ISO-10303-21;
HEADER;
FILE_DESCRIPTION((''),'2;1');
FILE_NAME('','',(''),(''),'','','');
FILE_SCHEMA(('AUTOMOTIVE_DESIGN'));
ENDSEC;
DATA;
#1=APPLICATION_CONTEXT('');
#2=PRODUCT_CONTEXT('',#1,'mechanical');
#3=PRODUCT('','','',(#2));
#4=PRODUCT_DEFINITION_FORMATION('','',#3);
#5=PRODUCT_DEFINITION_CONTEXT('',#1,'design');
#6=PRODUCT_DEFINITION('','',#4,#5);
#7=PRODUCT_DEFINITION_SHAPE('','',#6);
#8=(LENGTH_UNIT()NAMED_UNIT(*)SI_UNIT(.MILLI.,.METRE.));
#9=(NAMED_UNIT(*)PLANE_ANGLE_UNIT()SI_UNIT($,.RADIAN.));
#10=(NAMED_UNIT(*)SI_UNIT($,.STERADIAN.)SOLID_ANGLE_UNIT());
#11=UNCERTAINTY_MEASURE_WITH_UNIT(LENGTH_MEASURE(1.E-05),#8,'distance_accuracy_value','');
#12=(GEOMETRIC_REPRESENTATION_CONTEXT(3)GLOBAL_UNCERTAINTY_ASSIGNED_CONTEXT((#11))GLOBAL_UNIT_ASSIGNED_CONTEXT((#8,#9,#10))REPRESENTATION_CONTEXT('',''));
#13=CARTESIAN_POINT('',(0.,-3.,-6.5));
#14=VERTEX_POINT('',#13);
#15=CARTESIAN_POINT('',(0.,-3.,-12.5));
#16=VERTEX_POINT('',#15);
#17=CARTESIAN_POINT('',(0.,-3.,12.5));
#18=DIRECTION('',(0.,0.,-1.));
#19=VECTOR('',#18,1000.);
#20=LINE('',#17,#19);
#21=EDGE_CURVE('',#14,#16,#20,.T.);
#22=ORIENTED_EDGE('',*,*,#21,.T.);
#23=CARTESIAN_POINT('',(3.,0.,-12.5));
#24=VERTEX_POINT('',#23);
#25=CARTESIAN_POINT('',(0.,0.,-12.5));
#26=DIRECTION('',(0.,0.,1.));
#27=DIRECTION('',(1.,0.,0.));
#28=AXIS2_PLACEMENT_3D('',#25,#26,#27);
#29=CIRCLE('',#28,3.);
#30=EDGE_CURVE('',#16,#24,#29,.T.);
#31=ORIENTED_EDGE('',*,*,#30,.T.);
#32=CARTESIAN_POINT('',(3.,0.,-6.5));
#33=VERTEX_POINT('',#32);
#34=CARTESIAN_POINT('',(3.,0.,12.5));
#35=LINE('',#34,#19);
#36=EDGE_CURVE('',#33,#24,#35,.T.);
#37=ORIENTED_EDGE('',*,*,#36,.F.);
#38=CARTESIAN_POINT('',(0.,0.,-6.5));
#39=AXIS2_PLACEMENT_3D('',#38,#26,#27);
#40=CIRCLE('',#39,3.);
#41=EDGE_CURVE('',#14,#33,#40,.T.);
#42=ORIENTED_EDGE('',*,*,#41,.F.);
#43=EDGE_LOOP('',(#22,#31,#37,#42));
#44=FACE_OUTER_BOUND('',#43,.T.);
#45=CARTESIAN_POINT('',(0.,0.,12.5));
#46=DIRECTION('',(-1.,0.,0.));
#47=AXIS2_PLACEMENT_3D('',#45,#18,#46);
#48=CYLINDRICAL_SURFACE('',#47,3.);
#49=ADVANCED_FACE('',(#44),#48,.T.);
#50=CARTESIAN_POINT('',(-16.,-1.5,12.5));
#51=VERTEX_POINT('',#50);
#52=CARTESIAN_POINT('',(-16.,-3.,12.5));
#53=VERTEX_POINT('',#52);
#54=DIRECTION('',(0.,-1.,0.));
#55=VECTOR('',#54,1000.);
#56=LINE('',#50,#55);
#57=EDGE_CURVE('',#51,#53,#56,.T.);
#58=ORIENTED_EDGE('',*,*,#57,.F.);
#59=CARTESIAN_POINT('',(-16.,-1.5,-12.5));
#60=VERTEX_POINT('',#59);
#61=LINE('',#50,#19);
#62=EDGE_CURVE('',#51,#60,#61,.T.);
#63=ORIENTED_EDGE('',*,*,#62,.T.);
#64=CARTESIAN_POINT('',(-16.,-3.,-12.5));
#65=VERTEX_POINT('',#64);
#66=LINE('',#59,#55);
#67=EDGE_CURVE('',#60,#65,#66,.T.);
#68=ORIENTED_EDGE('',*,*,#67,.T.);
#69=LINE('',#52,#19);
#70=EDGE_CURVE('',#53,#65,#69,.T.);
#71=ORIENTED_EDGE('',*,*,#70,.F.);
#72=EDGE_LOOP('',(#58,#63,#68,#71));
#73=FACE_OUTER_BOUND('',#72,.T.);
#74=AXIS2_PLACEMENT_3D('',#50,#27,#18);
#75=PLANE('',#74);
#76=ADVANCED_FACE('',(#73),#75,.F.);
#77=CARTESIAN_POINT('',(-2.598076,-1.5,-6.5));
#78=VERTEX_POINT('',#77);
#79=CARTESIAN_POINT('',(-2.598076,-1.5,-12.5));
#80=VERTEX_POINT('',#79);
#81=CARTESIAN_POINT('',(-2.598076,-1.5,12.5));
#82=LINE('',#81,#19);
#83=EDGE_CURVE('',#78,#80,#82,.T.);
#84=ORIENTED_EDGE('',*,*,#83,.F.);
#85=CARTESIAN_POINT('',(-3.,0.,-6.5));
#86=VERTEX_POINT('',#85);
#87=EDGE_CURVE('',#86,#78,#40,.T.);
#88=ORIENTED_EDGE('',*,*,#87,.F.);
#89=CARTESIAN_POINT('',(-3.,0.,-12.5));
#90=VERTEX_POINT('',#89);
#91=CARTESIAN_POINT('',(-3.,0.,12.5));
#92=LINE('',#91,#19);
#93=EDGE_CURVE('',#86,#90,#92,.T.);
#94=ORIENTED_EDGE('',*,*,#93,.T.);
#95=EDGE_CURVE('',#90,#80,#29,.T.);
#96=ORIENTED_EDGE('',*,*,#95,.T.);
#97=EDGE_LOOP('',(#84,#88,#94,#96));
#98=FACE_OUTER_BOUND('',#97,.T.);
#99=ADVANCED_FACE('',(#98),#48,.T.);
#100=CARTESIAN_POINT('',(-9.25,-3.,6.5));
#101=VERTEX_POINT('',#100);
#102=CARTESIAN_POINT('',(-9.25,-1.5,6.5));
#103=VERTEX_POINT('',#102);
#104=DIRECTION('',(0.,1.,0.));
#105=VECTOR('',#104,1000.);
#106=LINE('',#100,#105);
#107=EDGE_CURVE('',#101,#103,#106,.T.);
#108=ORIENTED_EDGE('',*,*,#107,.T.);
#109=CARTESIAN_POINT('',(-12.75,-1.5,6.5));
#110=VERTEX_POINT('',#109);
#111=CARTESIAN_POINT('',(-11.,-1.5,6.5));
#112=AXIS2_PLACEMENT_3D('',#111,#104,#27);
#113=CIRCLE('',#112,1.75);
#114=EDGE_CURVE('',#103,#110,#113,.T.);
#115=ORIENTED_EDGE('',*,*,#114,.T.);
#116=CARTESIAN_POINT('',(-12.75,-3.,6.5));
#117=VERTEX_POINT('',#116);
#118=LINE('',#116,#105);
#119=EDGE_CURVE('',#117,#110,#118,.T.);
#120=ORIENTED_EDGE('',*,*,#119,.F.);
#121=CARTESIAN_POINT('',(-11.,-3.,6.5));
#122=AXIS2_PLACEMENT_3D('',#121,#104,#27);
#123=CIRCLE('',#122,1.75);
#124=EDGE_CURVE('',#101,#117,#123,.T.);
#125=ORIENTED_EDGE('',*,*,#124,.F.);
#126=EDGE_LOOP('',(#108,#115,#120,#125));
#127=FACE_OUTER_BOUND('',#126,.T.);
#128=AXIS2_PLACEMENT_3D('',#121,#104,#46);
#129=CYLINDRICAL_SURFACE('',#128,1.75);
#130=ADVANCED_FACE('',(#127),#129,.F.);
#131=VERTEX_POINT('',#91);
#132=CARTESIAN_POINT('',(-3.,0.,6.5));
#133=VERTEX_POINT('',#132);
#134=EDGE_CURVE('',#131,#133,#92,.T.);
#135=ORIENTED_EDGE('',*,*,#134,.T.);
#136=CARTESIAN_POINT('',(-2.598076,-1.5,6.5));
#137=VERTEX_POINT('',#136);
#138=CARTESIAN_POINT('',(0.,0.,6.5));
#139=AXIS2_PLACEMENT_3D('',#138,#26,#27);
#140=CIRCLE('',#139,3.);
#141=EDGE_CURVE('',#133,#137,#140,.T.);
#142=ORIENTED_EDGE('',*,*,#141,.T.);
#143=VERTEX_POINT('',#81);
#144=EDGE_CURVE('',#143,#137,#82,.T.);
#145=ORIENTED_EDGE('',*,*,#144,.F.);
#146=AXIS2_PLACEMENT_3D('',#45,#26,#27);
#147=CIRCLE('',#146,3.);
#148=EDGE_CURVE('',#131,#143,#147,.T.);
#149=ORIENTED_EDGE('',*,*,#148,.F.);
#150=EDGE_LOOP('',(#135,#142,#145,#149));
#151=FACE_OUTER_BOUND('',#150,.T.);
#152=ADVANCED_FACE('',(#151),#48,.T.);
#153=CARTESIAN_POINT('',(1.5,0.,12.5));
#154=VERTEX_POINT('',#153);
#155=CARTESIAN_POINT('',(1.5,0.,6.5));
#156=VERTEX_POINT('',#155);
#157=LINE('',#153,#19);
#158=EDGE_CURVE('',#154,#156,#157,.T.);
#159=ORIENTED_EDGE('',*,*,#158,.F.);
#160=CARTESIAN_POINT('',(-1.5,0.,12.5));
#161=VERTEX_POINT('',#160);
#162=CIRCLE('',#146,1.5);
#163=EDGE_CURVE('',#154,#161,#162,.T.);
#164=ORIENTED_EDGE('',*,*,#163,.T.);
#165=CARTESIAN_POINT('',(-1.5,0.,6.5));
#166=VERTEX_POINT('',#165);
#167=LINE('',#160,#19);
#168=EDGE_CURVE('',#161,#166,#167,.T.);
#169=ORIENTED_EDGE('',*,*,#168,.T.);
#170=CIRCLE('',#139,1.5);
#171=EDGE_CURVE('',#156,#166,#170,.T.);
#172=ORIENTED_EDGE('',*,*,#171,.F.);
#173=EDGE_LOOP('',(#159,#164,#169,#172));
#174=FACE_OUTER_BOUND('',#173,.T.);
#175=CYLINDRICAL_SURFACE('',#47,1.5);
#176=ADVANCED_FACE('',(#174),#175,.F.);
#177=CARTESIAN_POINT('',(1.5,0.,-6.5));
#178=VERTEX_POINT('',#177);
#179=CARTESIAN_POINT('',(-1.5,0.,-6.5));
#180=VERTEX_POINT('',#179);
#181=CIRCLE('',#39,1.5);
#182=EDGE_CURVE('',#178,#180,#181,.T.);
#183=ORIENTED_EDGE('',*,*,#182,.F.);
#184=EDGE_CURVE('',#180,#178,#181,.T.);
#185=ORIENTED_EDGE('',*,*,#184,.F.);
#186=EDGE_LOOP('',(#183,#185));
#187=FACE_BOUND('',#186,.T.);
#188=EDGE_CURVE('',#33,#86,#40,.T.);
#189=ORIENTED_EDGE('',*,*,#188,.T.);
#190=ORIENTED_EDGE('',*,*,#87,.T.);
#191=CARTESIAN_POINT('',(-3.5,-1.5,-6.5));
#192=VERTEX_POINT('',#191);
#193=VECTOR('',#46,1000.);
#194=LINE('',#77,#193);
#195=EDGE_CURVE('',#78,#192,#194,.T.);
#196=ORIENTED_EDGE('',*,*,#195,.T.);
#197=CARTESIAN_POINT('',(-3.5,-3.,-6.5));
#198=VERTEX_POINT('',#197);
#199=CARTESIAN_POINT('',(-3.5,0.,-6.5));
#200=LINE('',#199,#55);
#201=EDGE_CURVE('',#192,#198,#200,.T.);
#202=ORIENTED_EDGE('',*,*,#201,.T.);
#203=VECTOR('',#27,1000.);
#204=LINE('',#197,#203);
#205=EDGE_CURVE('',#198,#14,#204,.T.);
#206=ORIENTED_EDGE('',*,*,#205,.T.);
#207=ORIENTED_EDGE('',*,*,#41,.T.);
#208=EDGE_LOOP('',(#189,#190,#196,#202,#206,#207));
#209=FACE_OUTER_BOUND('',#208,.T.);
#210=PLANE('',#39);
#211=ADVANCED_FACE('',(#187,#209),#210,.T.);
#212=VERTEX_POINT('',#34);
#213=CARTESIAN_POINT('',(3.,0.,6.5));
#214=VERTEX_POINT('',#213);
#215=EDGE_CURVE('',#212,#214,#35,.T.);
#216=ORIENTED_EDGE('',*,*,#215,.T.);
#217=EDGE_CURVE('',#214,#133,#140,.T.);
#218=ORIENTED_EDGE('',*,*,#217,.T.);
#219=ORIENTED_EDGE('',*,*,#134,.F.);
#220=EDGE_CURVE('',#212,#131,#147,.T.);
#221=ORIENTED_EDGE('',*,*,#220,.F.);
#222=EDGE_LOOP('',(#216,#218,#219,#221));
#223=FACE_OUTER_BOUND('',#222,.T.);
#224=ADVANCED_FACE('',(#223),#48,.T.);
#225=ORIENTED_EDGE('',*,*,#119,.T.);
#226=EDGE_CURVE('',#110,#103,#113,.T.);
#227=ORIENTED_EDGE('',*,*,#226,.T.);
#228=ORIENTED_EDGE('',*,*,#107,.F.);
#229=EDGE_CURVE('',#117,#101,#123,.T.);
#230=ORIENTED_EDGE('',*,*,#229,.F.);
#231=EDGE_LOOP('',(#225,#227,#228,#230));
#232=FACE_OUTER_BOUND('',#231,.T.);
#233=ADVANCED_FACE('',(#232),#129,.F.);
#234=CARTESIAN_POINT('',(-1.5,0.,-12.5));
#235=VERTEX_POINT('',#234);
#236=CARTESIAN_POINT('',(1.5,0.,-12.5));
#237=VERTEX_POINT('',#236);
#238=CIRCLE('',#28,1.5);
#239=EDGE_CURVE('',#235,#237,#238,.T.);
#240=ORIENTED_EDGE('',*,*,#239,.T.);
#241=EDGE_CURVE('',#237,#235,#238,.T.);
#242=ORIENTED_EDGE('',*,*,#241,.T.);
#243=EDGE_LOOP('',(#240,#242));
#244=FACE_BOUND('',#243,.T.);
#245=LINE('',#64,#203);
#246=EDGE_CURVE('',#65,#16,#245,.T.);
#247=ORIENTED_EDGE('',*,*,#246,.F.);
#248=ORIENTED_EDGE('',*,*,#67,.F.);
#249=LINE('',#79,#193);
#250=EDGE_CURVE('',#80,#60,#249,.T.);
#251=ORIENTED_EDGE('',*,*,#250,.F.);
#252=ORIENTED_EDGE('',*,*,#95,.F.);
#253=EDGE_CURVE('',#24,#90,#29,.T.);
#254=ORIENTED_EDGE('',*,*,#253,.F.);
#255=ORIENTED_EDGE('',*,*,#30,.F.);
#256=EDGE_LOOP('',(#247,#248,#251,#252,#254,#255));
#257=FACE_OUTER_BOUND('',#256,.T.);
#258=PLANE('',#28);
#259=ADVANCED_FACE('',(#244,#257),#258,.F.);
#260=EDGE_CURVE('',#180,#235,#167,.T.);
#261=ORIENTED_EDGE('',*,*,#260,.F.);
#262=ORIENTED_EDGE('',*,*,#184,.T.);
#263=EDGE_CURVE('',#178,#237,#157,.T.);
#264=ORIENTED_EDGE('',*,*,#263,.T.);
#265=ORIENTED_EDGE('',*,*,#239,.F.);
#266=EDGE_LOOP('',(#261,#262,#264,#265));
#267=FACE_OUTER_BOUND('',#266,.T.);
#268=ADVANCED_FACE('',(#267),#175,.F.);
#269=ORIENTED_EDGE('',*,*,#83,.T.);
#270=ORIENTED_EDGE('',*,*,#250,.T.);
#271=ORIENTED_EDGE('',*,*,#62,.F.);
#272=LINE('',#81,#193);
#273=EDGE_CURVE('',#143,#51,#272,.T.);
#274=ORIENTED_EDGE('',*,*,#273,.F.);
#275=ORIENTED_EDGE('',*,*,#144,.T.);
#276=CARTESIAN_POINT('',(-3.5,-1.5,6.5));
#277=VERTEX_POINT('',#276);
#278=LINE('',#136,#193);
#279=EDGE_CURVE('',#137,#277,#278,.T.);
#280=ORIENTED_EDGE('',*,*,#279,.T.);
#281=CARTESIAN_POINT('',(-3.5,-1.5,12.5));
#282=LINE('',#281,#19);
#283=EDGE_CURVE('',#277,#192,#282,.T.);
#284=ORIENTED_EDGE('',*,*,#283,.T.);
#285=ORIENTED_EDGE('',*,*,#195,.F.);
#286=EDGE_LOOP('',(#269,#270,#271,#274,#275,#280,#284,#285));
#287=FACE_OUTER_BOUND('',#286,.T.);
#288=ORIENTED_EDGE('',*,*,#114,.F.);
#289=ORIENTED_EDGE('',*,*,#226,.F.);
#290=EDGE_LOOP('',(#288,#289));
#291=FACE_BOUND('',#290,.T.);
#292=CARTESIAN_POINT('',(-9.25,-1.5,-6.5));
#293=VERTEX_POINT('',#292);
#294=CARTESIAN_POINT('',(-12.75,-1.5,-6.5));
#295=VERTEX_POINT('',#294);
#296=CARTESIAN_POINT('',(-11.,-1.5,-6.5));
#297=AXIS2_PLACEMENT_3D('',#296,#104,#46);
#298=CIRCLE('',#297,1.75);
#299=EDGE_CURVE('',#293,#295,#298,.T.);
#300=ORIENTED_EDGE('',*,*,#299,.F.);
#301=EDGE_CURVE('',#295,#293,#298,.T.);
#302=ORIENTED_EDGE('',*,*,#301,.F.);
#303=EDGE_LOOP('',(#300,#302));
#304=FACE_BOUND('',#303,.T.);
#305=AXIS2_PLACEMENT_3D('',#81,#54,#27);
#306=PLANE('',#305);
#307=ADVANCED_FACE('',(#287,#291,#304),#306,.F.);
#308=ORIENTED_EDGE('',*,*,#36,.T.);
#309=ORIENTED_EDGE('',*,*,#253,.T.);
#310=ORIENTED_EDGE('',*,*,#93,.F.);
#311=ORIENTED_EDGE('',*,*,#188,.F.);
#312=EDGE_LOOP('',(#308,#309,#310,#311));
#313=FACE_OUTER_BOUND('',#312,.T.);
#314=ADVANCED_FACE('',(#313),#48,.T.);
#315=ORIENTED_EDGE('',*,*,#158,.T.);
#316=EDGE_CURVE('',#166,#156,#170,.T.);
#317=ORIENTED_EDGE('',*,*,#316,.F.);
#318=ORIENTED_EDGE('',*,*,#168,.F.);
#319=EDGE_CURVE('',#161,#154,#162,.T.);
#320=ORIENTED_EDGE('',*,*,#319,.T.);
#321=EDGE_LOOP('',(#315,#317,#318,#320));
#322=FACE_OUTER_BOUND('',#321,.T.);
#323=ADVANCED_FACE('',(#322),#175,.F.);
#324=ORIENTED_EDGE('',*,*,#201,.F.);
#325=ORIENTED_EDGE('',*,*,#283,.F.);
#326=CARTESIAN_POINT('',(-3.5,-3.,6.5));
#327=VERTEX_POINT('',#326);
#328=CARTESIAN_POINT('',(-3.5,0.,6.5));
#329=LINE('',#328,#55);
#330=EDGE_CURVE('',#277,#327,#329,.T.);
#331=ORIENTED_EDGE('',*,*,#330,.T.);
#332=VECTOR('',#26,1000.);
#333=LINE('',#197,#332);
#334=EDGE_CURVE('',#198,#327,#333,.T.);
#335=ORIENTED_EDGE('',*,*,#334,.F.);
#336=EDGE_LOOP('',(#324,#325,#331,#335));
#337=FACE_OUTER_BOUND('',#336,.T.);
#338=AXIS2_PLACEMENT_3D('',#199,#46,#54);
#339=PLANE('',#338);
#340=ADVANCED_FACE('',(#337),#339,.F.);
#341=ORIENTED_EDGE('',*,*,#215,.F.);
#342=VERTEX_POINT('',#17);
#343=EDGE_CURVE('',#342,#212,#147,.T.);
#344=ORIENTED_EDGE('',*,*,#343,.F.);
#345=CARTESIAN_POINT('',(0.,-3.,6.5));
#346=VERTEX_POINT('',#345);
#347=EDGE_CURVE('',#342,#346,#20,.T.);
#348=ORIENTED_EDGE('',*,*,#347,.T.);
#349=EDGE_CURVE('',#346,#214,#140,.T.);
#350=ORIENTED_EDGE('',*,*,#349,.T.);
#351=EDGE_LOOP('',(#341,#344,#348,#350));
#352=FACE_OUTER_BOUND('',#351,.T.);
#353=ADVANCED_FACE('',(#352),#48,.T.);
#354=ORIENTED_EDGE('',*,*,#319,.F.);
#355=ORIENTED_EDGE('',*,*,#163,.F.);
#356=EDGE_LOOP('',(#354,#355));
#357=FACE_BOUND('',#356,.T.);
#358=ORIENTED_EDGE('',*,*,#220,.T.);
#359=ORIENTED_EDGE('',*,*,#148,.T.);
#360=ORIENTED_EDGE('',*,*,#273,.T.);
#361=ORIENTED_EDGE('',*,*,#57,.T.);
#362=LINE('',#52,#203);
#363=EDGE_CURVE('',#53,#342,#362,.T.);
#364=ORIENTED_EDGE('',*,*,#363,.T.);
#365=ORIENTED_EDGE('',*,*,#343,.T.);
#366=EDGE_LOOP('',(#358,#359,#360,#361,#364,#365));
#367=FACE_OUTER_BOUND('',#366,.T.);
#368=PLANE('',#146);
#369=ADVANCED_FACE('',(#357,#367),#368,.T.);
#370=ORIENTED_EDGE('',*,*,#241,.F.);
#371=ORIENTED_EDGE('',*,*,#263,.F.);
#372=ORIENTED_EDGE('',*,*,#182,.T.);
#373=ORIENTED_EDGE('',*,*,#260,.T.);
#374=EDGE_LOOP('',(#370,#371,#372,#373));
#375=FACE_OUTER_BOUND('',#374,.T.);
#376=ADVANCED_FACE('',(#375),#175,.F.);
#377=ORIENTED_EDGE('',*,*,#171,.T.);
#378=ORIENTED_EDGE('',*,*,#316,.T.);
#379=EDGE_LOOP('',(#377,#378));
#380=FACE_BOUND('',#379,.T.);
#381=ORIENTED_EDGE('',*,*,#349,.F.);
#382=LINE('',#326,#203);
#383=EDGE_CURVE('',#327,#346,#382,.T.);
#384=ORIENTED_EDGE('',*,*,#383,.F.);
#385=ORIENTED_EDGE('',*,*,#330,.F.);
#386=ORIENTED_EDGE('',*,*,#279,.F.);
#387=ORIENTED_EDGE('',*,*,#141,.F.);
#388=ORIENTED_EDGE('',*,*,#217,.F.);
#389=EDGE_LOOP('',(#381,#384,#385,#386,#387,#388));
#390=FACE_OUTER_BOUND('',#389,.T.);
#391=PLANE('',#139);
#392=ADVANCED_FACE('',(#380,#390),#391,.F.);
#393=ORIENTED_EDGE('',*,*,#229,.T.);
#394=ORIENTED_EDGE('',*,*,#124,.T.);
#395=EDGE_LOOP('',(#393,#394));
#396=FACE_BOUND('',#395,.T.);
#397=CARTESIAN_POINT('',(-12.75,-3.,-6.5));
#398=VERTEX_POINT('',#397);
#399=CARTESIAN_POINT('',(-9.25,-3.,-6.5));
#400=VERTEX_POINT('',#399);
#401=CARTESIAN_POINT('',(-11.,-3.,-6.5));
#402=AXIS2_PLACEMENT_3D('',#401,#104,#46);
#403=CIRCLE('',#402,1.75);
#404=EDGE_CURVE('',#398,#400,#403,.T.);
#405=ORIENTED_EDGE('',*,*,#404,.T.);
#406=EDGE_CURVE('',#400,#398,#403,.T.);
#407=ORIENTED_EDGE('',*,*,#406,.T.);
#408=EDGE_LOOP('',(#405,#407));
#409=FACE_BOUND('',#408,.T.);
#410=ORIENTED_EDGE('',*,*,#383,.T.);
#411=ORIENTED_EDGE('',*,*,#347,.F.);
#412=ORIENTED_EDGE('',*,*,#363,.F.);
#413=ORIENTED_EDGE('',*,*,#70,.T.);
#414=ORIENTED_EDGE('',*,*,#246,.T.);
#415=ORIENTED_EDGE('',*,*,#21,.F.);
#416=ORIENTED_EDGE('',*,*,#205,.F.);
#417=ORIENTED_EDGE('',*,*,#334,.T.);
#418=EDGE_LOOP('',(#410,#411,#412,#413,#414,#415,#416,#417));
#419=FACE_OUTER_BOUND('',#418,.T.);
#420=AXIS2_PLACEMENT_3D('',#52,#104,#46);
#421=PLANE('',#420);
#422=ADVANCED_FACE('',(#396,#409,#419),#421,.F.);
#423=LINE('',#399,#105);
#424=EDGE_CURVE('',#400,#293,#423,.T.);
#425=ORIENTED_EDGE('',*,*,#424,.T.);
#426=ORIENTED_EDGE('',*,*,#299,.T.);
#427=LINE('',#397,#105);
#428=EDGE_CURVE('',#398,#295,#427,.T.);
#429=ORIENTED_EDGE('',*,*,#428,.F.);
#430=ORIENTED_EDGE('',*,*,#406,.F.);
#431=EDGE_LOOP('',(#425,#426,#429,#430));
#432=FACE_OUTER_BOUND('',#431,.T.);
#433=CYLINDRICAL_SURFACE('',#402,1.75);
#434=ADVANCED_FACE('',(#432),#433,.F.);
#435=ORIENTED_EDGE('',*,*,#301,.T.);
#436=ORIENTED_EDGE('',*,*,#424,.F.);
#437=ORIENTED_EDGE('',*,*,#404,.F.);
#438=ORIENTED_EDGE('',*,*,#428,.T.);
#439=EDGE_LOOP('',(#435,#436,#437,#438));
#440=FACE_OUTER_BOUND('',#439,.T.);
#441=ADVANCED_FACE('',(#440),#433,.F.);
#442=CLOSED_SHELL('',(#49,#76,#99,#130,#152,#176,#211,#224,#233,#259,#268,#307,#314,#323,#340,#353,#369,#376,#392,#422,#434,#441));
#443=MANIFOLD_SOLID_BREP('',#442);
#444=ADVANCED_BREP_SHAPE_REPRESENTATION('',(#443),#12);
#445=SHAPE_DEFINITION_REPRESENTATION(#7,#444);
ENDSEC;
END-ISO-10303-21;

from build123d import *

# Parameters (mm, degrees)
SKETCH_1_R          = 1.5
EXTRUDE_1_DEPTH     = 12.5
CUT_EXTRUDE_1_DEPTH = 6.5
SKETCH_3_R          = 1.75
CUT_EXTRUDE_2_DEPTH = 21.796634343


with BuildPart() as part:
    # 草图1 → 凸台-拉伸1 (new, symmetric)
    with BuildSketch(Plane.XY):
        with BuildLine():
            Line((-2.598076211, -1.5), (-16, -1.5))
            Line((-16, -1.5), (-16, -3))
            Line((-16, -3), (0, -3))
            ThreePointArc((0, -3), (1.5, 2.598076211), (-2.598076211, -1.5))
        make_face()
        Circle(SKETCH_1_R, mode=Mode.SUBTRACT)
    extrude(amount=EXTRUDE_1_DEPTH, both=True)

    # 草图2 → 切除-拉伸1 (cut, symmetric)
    with BuildSketch(Plane.XY):
        with BuildLine():
            Line((-3.5, 0), (-3.5, -3))
            Line((-3.5, -3), (-1.802775638, -3))
            ThreePointArc((-1.802775638, -3), (3.046285831, 1.723410176), (-3.5, 0))
        make_face()
    extrude(amount=CUT_EXTRUDE_1_DEPTH, both=True, mode=Mode.SUBTRACT)

    # 草图3 → 切除-拉伸2 (cut, through all)
    with BuildSketch(Plane(origin=(0, -1.5, 0), x_dir=(1, 0, 0), z_dir=(0, 1, 0))):
        with Locations(Location((-11, 6.5, 0), (0, 0, 180))):
            Circle(SKETCH_3_R)
        with Locations((-11, -6.5)):
            Circle(SKETCH_3_R)
    extrude(amount=-CUT_EXTRUDE_2_DEPTH, mode=Mode.SUBTRACT)


solid = part.part
